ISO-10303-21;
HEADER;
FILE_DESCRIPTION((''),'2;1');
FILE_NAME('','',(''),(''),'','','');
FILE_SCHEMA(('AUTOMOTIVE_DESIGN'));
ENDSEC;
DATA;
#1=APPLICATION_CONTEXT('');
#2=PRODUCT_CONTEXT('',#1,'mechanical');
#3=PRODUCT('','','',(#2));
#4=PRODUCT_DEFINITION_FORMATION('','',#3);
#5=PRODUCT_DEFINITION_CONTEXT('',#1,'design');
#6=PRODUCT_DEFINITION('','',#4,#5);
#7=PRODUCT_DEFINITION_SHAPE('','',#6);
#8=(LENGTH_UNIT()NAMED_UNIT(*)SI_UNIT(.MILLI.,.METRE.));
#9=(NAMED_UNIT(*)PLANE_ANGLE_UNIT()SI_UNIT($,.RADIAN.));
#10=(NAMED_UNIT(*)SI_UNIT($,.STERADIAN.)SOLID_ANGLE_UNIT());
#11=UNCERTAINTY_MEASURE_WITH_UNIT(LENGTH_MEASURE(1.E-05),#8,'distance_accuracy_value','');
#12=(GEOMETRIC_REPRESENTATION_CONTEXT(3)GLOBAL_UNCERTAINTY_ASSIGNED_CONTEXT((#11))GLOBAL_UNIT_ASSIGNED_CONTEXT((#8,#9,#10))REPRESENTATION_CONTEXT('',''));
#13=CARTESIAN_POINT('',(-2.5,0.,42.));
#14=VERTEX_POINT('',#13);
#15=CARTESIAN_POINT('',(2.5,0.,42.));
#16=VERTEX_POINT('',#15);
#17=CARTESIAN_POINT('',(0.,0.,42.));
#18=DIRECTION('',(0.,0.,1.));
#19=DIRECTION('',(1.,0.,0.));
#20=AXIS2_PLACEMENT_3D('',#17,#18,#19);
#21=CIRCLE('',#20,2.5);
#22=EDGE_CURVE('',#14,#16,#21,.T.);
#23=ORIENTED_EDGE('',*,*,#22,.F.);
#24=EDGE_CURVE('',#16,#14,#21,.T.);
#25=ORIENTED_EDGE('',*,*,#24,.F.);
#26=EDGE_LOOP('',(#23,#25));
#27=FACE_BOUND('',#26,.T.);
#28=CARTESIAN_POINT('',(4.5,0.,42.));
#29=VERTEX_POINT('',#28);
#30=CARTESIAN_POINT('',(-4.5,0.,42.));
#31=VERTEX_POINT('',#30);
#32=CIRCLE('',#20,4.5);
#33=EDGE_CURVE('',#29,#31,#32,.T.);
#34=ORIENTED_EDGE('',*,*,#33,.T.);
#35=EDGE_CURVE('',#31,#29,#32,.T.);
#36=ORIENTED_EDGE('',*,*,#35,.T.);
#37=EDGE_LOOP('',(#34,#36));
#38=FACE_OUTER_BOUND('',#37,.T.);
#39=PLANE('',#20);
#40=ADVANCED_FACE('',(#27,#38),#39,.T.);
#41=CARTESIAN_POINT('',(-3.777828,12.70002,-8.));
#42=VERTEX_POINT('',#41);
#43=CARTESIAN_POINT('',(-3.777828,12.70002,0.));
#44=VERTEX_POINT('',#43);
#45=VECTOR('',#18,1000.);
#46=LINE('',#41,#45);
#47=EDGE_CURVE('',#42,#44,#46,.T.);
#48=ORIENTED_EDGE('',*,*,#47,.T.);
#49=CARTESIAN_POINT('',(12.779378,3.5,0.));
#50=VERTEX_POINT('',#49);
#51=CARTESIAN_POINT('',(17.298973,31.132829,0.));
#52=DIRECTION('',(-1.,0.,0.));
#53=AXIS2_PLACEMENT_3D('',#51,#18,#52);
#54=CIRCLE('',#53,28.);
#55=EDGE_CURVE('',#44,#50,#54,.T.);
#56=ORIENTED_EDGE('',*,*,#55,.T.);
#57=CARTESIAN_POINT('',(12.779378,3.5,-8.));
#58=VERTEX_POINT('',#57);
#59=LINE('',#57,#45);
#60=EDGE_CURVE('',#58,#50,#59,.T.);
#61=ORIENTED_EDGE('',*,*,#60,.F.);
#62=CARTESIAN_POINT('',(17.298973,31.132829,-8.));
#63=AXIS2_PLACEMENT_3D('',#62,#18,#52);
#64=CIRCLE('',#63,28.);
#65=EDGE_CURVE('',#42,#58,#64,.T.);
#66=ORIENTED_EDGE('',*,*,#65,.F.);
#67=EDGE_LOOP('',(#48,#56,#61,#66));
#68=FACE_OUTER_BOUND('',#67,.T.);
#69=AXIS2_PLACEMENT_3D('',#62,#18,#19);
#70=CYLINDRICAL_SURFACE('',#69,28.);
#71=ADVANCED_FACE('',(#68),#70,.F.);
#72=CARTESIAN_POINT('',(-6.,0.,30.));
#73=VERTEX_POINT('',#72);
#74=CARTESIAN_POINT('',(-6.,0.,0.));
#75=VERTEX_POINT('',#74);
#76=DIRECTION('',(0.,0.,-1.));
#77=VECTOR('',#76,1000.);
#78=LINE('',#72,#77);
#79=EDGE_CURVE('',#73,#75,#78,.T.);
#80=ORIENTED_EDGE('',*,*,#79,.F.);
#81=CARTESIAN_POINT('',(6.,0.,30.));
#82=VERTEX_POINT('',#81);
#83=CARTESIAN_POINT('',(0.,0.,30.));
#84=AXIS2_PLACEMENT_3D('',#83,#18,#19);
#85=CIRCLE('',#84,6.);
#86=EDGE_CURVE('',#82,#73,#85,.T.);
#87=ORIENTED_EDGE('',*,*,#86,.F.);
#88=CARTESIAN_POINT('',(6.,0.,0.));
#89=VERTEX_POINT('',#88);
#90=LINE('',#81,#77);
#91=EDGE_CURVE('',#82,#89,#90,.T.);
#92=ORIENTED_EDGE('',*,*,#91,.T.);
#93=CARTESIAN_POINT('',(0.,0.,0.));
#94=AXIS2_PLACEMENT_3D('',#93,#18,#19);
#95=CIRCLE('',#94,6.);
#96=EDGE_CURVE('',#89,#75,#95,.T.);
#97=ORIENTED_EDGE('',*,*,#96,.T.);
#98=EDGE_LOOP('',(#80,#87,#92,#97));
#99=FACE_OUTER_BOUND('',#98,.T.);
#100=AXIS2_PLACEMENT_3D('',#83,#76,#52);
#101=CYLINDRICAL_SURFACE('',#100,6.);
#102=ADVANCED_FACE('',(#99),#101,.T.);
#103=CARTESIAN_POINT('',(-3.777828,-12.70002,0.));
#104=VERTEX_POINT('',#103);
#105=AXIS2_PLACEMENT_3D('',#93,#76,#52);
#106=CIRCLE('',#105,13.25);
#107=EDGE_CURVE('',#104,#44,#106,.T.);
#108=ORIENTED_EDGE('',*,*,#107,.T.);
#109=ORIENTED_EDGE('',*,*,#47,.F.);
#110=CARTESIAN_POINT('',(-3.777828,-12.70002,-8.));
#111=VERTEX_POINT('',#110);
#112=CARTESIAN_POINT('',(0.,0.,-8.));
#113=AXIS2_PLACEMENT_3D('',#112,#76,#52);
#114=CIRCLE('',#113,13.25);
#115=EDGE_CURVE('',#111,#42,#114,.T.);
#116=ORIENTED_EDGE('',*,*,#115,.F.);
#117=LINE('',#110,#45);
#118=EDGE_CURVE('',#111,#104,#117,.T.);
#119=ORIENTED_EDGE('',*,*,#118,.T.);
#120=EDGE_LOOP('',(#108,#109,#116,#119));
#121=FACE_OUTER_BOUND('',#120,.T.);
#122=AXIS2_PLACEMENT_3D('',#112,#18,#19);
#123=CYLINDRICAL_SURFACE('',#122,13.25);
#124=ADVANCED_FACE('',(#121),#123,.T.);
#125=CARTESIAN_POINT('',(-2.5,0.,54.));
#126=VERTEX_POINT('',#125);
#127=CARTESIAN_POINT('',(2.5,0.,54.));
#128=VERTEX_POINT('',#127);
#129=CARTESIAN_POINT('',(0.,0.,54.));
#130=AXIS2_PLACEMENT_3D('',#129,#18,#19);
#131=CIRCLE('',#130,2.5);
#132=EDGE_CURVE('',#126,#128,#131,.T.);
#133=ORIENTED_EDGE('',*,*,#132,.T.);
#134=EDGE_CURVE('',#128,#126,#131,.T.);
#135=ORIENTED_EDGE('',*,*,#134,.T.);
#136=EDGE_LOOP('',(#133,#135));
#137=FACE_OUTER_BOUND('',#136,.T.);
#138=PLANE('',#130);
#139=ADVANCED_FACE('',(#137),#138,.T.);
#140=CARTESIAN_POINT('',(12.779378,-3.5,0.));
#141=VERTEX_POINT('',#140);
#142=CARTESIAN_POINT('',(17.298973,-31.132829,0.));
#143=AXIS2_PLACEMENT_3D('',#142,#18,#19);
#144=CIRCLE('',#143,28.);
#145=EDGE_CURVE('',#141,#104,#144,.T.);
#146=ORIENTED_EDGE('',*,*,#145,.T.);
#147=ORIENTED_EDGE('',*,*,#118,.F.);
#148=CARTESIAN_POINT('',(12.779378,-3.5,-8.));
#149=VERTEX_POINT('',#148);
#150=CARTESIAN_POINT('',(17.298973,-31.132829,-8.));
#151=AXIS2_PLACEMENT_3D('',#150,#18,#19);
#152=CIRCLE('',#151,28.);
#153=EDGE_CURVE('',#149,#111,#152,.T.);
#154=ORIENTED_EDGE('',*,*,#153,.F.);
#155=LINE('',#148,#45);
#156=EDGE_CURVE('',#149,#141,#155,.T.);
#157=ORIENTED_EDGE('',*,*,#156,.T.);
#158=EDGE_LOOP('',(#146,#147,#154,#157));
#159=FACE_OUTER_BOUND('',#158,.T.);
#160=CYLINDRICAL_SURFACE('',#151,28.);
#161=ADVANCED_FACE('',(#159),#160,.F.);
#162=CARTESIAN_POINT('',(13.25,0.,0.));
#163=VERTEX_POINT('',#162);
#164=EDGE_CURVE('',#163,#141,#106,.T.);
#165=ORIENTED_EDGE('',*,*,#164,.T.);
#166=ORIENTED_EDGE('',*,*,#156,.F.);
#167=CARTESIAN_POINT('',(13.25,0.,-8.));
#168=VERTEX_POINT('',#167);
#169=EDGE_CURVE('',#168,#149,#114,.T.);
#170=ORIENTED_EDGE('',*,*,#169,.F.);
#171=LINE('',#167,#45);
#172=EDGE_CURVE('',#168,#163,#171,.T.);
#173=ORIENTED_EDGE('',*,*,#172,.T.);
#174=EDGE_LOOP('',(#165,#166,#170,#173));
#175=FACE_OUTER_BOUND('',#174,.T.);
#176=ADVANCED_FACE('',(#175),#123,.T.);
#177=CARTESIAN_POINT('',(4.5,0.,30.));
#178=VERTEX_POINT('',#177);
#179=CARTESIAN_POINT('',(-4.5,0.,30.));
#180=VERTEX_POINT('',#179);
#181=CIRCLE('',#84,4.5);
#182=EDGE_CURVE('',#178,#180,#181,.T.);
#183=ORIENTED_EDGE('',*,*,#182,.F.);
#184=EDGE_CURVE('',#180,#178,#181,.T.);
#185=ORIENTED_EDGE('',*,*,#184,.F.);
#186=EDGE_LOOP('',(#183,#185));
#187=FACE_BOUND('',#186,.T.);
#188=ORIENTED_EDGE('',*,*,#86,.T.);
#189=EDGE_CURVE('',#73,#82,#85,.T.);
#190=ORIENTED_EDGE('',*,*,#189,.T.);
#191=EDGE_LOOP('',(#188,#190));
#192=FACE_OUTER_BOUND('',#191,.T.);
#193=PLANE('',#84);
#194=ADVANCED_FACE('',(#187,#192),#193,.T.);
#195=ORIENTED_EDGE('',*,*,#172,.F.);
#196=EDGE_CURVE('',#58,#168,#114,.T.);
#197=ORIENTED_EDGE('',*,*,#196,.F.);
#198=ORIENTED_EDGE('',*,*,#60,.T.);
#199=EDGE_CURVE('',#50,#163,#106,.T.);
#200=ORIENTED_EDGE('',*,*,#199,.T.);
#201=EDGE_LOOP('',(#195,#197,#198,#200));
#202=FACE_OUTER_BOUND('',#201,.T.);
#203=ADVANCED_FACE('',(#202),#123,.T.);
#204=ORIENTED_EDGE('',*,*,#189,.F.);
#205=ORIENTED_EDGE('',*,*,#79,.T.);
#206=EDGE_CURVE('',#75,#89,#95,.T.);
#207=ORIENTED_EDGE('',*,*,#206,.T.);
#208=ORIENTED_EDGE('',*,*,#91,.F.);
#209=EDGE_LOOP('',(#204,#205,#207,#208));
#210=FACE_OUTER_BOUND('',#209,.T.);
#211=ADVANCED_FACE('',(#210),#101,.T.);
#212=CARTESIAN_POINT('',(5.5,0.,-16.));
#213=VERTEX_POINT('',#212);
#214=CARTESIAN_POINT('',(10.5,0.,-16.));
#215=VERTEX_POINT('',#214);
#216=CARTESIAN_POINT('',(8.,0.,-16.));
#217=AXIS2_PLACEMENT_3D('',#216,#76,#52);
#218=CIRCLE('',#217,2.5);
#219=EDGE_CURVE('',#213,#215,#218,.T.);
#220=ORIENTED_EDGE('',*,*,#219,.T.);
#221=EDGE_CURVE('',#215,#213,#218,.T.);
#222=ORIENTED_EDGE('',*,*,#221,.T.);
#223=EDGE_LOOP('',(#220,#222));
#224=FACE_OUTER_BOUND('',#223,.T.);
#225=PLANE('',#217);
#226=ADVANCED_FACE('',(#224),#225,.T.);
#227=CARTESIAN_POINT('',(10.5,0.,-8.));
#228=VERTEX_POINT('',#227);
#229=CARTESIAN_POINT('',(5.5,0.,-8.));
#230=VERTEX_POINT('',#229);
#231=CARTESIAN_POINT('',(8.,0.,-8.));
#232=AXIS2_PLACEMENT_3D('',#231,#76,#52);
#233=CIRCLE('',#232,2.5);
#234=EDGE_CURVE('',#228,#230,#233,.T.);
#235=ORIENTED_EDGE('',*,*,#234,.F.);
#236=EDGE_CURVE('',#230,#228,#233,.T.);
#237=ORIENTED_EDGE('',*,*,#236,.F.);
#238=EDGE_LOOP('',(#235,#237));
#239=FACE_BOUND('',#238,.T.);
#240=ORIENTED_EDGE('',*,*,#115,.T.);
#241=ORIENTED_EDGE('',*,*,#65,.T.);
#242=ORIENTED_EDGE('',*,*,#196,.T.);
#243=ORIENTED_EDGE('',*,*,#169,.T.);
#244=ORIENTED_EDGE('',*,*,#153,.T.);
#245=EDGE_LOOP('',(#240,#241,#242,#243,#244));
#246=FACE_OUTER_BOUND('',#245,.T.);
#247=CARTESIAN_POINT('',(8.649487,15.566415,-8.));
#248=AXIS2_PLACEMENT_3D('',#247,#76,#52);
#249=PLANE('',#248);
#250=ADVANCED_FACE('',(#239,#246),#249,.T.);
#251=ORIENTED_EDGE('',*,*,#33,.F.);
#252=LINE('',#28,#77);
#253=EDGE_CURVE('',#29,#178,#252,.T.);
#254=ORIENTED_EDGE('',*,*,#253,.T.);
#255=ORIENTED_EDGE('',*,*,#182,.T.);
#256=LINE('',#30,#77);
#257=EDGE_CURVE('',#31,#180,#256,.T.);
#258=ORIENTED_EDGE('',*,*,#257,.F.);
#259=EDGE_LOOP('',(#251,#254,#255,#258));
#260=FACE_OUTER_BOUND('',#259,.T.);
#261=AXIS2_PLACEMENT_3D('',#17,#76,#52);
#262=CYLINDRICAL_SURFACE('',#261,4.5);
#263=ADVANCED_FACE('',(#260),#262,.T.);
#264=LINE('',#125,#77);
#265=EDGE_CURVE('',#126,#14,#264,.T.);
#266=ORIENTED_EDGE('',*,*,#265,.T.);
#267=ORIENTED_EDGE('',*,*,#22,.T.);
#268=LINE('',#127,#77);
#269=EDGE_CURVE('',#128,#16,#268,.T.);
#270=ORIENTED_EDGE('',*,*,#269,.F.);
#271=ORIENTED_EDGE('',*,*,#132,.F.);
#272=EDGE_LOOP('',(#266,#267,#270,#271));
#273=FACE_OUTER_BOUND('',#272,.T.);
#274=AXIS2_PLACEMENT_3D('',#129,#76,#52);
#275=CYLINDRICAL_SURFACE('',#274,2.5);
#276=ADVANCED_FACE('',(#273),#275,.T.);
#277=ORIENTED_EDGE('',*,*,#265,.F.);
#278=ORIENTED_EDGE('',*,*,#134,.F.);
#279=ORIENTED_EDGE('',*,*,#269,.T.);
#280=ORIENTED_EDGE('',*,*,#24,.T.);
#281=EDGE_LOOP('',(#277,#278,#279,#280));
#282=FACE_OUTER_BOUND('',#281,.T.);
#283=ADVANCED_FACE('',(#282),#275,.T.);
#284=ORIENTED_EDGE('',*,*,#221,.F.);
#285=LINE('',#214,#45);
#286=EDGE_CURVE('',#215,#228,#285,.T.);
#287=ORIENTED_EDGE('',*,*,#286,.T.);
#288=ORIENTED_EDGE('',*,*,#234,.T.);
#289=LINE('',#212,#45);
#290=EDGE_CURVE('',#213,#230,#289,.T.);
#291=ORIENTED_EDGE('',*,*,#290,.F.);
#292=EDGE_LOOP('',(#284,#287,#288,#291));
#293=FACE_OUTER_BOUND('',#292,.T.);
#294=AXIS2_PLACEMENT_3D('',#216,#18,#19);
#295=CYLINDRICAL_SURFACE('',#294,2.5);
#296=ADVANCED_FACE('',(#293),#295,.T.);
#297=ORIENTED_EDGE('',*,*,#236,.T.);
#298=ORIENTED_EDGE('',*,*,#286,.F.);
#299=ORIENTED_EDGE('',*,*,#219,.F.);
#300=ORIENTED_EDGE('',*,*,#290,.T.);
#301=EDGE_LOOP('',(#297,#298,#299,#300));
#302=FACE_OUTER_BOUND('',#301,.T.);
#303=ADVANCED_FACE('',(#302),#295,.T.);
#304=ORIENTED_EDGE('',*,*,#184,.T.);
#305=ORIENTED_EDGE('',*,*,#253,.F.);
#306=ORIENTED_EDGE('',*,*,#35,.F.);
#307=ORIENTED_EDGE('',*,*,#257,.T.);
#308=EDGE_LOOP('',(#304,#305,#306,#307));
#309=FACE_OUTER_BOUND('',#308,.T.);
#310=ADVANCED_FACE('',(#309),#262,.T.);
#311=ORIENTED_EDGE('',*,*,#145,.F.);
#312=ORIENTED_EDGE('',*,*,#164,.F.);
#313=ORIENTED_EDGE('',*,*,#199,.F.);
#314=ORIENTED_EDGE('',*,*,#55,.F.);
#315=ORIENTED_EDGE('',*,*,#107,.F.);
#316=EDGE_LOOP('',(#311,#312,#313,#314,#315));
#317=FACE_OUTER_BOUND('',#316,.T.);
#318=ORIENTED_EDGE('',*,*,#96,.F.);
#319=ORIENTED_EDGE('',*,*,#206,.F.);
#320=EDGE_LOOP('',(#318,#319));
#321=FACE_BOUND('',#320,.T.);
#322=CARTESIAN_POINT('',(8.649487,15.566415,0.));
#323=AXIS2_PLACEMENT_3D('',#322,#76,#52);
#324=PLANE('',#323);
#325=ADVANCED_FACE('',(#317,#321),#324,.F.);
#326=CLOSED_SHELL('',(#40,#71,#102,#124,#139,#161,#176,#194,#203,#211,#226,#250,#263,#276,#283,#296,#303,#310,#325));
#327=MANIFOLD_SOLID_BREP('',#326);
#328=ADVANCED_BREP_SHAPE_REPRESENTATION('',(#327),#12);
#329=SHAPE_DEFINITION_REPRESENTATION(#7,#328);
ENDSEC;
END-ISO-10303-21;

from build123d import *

# Parameters (mm, degrees)
MAIN_JOURNAL_PROFILE_12_R = 6
MAIN_JOURNAL_12_DEPTH     = 30
STEP_JOURNAL_PROFILE_9_R  = 4.5
STEP_JOURNAL_9_DEPTH      = 12
SHAFT_END_PROFILE_5_R     = 2.5
SHAFT_END_5_DEPTH         = 12
CRANK_WEB_DEPTH           = 8
CRANK_PIN_PROFILE_R       = 2.5
CRANK_PIN_DEPTH           = 8


with BuildPart() as part:
    # Main Journal Profile Ø12 → Main Journal Ø12 (new body)
    with BuildSketch(Plane.XY):
        Circle(MAIN_JOURNAL_PROFILE_12_R)
    extrude(amount=MAIN_JOURNAL_12_DEPTH)

    # Step Journal Profile Ø9 → Step Journal Ø9 (add)
    with BuildSketch(Plane.XY.offset(30)):
        Circle(STEP_JOURNAL_PROFILE_9_R)
    extrude(amount=STEP_JOURNAL_9_DEPTH)

    # Shaft End Profile Ø5 → Shaft End Ø5 (add)
    with BuildSketch(Plane.XY.offset(42)):
        Circle(SHAFT_END_PROFILE_5_R)
    extrude(amount=SHAFT_END_5_DEPTH)

    # Crank Web Profile → Crank Web (add)
    with BuildSketch(Plane(origin=(0, 0, 0), x_dir=(-1, 0, 0), z_dir=(0, 0, -1))):
        with BuildLine():
            ThreePointArc((-12.779377919, 3.5), (-13.25, 0), (-12.779377919, -3.5))
            ThreePointArc((-12.779377919, -3.5), (-3.699194839, -6.657412557), (3.777827997, -12.7000203))
            ThreePointArc((3.777827997, -12.7000203), (13.25, 0), (3.777827997, 12.7000203))
            ThreePointArc((3.777827997, 12.7000203), (-3.699194839, 6.657412557), (-12.779377919, 3.5))
        make_face()
    extrude(amount=CRANK_WEB_DEPTH)

    # Crank Pin Profile → Crank Pin (add)
    with BuildSketch(Plane(origin=(0, 0, -8), x_dir=(-1, 0, 0), z_dir=(0, 0, -1))):
        with Locations((-8, 0)):
            Circle(CRANK_PIN_PROFILE_R)
    extrude(amount=CRANK_PIN_DEPTH)


solid = part.part
